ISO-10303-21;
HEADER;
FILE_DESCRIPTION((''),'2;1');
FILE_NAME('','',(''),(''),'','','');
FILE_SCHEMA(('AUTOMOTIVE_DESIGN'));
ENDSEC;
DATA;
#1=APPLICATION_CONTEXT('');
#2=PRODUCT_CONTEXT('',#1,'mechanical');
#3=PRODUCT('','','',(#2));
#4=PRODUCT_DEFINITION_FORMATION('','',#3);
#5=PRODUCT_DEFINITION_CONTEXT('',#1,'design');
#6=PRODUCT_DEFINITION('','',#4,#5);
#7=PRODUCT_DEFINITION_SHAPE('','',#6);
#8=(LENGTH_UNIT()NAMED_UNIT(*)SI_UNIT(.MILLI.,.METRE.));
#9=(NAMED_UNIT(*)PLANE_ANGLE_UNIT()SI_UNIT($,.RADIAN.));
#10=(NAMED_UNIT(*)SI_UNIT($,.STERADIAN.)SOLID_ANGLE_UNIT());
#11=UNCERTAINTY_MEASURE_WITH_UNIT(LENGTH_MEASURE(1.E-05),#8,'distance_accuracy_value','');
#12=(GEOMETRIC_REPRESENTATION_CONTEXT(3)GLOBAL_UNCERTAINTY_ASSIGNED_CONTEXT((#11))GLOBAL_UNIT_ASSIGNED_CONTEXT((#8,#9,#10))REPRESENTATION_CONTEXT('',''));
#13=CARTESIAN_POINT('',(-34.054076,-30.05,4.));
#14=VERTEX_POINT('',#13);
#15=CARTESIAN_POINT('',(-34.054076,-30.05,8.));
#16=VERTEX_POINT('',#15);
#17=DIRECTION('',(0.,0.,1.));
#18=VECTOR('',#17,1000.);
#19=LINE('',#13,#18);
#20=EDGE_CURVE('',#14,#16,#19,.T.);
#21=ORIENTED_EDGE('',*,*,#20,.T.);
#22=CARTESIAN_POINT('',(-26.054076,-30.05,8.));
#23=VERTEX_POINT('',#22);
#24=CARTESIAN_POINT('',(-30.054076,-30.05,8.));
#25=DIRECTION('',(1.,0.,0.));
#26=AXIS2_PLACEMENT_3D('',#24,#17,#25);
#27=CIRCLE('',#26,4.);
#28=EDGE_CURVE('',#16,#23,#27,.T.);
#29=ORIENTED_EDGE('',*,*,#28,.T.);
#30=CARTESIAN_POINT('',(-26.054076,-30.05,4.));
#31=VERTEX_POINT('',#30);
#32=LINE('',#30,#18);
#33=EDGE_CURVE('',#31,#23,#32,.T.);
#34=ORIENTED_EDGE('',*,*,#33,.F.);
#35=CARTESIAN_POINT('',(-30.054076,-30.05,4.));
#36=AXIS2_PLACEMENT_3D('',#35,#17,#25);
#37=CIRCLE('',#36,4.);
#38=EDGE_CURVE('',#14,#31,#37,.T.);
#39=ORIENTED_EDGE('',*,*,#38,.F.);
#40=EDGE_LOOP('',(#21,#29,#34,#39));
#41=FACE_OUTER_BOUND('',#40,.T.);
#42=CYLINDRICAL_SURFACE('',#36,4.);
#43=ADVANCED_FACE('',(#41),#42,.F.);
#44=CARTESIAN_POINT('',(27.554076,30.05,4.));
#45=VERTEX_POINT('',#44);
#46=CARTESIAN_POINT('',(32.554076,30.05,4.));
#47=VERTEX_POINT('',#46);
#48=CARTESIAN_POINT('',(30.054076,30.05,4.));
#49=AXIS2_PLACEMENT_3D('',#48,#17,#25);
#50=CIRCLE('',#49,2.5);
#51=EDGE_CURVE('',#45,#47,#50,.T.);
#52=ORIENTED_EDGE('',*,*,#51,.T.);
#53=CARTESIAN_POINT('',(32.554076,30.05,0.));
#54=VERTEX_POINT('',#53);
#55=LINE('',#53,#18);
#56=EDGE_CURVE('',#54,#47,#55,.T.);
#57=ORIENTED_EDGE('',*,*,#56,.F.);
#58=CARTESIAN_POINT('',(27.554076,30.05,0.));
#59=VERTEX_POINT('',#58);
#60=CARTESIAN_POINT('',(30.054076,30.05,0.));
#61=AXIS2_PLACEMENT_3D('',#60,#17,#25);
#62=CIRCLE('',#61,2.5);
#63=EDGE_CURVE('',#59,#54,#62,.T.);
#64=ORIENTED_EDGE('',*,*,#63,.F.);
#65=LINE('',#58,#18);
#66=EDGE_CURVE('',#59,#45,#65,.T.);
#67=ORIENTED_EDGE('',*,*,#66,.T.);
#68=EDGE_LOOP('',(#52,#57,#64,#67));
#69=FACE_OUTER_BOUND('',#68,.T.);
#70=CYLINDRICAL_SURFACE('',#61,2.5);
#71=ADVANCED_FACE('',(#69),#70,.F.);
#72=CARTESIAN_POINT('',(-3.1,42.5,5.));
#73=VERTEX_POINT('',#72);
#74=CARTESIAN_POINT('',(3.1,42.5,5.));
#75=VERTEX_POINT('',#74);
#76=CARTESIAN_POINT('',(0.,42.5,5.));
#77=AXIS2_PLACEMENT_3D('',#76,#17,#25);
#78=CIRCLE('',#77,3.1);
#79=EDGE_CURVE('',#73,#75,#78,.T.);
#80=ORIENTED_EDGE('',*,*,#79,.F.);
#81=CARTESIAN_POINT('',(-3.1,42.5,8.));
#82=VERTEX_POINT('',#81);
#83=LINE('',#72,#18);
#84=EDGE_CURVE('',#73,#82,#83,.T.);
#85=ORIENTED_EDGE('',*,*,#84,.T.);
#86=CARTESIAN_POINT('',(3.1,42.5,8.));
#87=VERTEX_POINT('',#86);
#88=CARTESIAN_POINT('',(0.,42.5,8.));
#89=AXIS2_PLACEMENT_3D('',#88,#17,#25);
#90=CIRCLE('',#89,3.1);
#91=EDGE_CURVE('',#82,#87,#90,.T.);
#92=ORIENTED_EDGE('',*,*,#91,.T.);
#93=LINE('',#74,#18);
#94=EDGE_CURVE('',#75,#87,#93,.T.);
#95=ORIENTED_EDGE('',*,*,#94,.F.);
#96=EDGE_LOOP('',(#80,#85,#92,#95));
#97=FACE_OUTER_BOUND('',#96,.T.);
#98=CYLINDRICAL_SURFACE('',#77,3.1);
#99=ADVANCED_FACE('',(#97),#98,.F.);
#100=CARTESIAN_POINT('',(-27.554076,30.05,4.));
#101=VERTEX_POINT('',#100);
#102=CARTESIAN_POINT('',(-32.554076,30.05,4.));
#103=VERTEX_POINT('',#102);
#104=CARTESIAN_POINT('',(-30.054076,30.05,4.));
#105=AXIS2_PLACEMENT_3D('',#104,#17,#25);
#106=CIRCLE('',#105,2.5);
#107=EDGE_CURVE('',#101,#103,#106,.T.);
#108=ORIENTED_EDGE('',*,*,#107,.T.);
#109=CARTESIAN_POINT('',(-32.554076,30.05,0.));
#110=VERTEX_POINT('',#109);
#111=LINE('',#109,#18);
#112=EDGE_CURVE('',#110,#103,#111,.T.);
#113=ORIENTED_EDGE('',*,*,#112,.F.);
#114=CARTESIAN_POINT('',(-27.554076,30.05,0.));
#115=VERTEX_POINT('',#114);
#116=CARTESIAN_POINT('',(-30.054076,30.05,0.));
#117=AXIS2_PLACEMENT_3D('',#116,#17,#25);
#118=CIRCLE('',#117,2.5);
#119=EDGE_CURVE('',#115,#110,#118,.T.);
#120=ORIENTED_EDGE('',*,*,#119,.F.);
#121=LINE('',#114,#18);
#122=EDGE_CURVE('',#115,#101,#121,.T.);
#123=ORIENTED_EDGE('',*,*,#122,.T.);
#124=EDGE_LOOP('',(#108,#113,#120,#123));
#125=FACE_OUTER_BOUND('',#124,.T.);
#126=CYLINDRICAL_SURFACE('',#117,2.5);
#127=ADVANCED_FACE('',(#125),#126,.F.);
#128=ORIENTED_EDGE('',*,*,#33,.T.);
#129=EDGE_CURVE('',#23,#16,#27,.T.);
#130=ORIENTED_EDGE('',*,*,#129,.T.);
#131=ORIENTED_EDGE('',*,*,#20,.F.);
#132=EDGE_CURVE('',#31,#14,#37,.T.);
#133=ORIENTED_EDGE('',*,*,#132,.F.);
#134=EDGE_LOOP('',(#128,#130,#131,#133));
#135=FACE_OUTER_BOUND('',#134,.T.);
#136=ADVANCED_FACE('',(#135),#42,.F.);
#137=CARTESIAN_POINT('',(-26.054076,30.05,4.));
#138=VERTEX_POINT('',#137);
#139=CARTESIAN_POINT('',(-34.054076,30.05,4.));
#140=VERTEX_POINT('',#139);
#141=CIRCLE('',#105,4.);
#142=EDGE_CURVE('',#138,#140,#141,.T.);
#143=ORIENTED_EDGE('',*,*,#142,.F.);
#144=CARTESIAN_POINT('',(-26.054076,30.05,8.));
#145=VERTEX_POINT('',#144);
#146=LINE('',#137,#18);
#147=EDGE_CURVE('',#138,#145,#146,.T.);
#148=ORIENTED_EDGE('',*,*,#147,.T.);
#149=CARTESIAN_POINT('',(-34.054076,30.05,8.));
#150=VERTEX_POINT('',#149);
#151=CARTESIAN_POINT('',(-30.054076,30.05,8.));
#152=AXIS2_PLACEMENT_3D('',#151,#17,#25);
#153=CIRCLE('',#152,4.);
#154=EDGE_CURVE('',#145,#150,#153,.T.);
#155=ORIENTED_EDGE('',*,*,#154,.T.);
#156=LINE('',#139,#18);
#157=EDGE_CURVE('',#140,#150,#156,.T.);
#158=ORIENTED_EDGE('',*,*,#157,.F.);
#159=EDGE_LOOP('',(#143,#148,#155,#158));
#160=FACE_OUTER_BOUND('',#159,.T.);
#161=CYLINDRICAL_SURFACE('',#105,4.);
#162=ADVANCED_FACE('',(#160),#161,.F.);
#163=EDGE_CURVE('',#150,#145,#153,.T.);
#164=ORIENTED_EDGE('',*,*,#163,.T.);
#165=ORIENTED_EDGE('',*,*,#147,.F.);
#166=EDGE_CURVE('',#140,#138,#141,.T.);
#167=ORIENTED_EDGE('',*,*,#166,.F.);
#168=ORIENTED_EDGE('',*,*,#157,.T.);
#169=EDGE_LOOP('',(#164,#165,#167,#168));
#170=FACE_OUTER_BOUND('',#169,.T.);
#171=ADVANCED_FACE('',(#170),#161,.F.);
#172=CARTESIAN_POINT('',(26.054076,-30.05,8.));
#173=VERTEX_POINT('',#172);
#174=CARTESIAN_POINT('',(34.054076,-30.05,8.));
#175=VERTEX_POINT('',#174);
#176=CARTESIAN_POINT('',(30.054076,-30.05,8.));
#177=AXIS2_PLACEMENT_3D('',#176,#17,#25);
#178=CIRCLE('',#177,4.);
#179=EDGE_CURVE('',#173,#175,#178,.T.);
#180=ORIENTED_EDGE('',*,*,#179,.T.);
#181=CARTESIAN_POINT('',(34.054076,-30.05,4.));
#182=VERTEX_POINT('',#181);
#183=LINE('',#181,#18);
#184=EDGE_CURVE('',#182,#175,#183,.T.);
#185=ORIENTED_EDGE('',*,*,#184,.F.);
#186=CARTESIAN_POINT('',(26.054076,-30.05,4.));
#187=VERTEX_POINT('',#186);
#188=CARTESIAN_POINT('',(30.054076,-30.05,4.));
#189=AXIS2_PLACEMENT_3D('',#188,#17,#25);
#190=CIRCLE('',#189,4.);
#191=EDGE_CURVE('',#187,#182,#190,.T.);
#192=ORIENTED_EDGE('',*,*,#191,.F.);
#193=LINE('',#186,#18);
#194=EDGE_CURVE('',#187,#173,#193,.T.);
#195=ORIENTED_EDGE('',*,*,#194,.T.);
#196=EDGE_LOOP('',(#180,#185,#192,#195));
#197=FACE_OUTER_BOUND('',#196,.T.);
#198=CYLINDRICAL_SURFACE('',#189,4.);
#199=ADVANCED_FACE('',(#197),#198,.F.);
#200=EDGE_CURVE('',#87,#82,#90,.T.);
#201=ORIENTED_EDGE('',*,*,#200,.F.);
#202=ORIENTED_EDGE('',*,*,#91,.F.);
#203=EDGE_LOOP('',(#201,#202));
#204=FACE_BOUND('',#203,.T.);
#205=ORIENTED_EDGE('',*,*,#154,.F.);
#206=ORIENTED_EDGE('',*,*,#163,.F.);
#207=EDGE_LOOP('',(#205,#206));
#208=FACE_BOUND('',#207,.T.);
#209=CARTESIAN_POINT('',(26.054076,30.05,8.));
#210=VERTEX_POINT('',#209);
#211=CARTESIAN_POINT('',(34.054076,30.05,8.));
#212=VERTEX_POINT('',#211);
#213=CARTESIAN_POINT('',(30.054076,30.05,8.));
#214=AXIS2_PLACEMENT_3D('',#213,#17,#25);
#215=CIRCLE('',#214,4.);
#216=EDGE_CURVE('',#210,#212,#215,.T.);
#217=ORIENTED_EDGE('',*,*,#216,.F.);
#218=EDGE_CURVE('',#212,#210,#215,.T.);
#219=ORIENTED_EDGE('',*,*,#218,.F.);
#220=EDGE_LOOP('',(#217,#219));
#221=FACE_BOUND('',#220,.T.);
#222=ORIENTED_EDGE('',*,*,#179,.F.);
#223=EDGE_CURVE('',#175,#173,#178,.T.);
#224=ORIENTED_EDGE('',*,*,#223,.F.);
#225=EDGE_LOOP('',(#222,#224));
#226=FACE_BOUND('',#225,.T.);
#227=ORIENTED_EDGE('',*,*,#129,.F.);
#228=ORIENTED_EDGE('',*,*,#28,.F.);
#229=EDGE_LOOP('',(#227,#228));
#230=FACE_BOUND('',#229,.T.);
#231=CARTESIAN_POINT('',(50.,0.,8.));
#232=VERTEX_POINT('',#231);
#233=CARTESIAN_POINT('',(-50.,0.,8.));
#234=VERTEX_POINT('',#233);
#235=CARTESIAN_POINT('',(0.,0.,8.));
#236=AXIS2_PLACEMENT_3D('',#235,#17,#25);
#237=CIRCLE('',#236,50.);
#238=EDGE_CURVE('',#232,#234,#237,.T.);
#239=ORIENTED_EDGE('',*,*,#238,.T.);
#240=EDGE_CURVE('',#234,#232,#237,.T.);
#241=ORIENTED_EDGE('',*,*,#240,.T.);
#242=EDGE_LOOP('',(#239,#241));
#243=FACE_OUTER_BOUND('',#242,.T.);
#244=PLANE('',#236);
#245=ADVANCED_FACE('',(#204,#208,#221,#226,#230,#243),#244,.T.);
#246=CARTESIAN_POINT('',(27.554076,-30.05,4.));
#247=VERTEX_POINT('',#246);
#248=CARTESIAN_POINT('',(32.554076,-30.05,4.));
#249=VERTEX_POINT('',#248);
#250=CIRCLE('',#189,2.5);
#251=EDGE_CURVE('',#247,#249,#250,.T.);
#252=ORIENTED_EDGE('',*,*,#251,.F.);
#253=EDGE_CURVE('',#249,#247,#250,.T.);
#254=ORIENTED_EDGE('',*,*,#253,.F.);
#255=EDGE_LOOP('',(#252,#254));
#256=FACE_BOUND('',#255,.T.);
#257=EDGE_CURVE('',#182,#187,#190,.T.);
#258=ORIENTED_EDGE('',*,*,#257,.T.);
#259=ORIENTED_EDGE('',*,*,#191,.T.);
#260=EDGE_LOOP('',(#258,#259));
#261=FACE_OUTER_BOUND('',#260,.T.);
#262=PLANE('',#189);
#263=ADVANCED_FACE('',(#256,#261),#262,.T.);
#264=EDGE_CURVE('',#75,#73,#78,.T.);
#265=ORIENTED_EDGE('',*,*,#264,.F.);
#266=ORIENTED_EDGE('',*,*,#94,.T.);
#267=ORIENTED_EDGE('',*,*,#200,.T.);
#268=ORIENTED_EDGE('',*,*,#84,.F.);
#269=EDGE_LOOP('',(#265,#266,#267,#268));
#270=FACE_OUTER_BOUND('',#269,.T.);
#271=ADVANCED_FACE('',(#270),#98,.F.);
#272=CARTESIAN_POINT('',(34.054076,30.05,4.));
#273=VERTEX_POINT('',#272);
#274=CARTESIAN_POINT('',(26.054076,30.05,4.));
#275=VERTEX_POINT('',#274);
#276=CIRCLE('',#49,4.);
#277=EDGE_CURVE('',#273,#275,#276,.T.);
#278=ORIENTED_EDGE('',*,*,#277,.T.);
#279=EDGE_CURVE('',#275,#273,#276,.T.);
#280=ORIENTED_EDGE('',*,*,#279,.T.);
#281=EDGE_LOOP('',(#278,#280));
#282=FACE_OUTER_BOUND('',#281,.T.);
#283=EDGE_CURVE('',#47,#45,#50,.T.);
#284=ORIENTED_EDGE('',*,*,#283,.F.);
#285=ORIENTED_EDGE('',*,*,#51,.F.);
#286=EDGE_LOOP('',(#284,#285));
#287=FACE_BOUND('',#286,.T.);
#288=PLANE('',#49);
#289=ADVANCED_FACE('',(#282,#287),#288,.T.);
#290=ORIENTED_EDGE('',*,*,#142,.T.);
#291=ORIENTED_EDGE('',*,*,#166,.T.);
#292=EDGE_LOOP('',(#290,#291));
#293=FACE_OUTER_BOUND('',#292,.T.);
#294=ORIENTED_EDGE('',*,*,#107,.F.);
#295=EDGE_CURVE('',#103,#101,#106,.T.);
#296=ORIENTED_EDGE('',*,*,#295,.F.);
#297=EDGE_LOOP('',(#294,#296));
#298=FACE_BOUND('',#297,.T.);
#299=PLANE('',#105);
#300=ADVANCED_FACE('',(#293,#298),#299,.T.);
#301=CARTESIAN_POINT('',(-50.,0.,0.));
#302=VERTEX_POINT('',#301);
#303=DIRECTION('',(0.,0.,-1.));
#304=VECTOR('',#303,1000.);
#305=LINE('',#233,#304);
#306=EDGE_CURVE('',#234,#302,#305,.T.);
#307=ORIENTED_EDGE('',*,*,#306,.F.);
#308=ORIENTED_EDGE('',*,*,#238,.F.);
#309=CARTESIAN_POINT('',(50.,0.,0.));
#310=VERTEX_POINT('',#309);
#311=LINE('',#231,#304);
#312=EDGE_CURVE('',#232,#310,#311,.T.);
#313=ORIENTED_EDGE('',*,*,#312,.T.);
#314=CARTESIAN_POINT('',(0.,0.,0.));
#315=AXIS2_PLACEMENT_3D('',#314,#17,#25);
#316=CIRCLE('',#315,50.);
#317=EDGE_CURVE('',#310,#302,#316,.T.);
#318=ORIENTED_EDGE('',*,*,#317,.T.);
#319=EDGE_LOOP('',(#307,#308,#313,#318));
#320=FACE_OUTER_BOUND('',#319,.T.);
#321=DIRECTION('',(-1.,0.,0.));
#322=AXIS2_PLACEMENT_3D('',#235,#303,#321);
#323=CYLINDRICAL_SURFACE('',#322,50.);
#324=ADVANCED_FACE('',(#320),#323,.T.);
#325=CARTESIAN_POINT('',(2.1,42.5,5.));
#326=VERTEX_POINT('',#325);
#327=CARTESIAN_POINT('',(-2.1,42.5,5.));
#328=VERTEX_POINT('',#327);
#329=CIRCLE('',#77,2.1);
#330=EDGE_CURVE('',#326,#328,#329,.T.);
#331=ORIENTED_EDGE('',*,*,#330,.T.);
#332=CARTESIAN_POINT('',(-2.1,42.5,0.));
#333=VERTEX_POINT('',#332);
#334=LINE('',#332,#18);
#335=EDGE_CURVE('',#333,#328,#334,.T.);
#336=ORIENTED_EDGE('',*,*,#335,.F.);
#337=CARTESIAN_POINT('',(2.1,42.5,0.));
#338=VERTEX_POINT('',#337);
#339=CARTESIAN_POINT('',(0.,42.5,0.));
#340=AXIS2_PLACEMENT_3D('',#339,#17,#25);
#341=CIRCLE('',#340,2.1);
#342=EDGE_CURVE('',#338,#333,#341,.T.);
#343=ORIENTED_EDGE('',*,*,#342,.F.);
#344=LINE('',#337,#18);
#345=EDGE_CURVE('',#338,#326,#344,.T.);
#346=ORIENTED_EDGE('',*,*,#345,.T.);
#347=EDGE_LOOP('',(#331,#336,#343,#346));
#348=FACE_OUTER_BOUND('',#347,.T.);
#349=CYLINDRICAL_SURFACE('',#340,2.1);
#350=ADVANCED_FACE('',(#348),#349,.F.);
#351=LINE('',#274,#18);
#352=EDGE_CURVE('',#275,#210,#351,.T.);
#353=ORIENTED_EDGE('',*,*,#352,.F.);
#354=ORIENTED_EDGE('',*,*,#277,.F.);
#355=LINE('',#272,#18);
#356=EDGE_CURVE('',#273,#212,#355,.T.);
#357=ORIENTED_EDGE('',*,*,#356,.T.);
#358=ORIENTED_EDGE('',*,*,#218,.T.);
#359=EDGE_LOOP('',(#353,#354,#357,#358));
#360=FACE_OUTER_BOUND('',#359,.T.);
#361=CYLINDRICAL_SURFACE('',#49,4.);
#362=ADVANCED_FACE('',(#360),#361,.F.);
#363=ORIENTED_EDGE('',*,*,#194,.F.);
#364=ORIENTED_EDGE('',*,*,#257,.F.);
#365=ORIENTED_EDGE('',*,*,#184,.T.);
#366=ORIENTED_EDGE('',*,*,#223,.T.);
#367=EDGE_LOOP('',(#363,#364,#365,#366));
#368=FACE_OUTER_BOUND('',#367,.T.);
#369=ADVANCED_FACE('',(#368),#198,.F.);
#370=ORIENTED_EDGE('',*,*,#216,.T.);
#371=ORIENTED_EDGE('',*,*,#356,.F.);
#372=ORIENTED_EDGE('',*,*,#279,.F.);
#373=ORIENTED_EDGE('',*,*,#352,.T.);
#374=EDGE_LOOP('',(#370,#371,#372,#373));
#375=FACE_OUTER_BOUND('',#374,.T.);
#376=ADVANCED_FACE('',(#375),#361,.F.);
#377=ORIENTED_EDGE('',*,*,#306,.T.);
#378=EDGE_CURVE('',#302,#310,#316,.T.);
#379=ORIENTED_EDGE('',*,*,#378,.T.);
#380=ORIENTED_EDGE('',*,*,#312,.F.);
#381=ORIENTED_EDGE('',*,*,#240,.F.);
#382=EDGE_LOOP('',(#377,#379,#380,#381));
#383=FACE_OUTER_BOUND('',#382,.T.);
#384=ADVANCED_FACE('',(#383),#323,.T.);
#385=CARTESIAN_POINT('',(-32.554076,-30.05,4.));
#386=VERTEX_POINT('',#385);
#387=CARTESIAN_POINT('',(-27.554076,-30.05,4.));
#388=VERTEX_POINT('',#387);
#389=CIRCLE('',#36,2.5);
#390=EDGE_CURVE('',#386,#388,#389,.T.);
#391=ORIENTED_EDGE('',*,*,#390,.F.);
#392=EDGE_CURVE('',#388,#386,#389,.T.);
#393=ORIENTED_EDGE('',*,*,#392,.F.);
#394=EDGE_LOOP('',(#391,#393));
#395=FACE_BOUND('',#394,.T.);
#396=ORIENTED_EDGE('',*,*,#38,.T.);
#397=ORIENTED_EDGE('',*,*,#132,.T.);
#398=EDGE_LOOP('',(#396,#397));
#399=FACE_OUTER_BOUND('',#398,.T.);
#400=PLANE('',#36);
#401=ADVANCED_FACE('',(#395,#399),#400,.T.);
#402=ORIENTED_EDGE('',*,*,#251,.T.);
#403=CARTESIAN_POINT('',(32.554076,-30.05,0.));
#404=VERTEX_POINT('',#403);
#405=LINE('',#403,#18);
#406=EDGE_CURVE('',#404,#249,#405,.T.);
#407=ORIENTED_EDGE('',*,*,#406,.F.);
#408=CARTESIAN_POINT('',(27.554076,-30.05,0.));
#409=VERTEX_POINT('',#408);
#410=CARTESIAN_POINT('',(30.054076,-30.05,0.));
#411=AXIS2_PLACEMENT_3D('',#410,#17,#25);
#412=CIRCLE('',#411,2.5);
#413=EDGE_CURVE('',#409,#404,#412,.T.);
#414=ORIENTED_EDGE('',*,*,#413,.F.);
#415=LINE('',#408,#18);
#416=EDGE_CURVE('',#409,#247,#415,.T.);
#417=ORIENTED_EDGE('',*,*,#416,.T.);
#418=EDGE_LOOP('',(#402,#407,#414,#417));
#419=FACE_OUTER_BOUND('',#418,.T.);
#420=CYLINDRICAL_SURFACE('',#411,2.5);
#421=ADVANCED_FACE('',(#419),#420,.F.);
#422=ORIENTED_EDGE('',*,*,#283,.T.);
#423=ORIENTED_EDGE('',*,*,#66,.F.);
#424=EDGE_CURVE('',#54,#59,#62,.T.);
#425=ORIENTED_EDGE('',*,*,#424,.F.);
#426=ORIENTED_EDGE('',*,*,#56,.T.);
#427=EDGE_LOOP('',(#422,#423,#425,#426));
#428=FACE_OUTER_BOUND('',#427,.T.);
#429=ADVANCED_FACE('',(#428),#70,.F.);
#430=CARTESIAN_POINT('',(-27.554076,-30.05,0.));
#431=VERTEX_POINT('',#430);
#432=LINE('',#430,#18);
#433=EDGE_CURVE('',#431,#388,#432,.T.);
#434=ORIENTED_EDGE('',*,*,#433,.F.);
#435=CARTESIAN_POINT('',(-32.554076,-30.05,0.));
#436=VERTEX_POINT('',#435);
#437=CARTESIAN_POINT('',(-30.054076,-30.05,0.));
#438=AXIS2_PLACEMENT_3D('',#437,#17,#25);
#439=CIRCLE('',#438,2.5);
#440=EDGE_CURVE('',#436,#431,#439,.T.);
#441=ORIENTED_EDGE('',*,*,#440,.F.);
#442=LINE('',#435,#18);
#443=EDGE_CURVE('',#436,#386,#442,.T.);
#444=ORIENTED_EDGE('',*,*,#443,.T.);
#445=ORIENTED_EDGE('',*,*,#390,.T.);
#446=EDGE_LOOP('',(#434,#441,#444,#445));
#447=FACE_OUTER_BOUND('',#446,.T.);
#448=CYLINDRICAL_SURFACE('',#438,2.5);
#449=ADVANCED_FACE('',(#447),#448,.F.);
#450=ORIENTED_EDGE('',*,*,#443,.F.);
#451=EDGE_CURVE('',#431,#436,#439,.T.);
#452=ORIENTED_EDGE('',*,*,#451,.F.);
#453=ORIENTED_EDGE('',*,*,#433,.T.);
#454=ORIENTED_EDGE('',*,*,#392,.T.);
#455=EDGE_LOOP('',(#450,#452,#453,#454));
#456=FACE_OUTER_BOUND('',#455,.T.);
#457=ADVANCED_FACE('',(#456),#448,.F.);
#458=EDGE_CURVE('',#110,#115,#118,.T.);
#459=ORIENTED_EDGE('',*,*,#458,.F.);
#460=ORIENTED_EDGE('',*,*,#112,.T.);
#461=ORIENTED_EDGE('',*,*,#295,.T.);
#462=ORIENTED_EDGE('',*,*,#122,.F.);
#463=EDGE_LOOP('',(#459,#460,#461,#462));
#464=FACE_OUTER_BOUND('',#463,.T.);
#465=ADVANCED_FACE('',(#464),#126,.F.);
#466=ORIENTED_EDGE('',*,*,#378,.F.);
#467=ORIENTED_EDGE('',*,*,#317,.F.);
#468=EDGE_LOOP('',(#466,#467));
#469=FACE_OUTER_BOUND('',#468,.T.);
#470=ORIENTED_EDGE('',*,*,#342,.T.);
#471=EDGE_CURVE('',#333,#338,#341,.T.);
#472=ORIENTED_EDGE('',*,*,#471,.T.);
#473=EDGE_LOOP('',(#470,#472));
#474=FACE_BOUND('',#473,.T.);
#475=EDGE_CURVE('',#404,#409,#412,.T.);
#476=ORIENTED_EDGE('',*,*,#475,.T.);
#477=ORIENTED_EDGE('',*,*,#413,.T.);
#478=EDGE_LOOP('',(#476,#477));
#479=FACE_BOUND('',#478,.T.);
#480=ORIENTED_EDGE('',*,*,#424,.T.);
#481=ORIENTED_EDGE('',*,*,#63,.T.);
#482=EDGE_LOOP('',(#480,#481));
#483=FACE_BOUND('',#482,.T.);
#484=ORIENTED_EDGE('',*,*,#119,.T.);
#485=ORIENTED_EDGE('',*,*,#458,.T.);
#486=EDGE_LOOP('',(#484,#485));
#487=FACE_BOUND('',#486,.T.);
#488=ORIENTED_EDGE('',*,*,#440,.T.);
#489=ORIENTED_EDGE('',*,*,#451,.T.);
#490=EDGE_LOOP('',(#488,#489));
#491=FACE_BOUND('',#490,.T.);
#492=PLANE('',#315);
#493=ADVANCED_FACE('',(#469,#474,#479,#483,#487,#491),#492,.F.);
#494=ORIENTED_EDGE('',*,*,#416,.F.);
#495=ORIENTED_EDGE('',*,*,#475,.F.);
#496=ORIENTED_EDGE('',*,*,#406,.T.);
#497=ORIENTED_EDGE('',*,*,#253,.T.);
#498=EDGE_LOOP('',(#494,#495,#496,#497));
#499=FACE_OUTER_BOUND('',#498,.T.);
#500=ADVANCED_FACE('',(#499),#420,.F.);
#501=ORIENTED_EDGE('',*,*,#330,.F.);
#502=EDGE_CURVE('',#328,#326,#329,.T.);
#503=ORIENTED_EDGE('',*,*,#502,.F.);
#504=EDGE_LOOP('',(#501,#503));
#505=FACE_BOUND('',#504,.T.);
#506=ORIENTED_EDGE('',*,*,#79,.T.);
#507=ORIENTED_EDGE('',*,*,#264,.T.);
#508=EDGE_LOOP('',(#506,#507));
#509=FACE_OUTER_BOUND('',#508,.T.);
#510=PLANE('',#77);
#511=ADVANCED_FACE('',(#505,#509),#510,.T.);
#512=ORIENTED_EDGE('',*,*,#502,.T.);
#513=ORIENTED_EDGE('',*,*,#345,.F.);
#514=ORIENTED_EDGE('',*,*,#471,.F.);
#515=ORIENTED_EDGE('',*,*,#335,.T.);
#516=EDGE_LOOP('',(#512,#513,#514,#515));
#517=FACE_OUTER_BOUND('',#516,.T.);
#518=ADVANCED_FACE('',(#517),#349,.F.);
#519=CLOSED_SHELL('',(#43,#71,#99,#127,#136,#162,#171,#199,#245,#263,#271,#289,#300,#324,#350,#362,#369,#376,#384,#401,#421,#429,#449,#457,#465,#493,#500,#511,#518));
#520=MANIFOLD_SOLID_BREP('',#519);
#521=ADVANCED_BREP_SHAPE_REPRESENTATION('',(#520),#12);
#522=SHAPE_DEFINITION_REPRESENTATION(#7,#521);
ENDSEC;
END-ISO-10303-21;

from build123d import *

# Parameters (mm, degrees)
SKETCH1_R           = 50
BOSS_EXTRUDE1_DEPTH = 8
SKETCH2_R           = 4
CUT_EXTRUDE1_DEPTH  = 4
SKETCH3_R           = 3.1
CUT_EXTRUDE2_DEPTH  = 3
SKETCH4_R           = 2.5
SKETCH4_R_2         = 2.1
CUT_EXTRUDE3_DEPTH  = 71.823724839
SKETCH5_R           = 2.1
CUT_EXTRUDE4_DEPTH  = 5


with BuildPart() as part:
    # Sketch1 → Boss-Extrude1 (new body)
    with BuildSketch(Plane.XY):
        Circle(SKETCH1_R)
    extrude(amount=BOSS_EXTRUDE1_DEPTH)

    # Sketch2 → Cut-Extrude1 (cut)
    with BuildSketch(Plane.XY.offset(8)):
        with Locations((-30.054076263, 30.05)):
            Circle(SKETCH2_R)
        with Locations((30.054076263, 30.05)):
            Circle(SKETCH2_R)
        with Locations((-30.054076263, -30.05)):
            Circle(SKETCH2_R)
        with Locations((30.054076263, -30.05)):
            Circle(SKETCH2_R)
    extrude(amount=-CUT_EXTRUDE1_DEPTH, mode=Mode.SUBTRACT)

    # Sketch3 → Cut-Extrude2 (cut)
    with BuildSketch(Plane.XY.offset(8)):
        with Locations((0, 42.5)):
            Circle(SKETCH3_R)
    extrude(amount=-CUT_EXTRUDE2_DEPTH, mode=Mode.SUBTRACT)

    # Sketch4 → Cut-Extrude3 (cut, through all)
    with BuildSketch(Plane.XY.offset(4)):
        with Locations((-30.054076263, 30.05)):
            Circle(SKETCH4_R)
        with Locations((30.054076263, 30.05)):
            Circle(SKETCH4_R)
        with Locations((-30.054076263, -30.05)):
            Circle(SKETCH4_R)
        with Locations((30.054076263, -30.05)):
            Circle(SKETCH4_R)
        with Locations((0, 42.5)):
            Circle(SKETCH4_R_2)
    extrude(amount=-CUT_EXTRUDE3_DEPTH, mode=Mode.SUBTRACT)

    # Sketch5 → Cut-Extrude4 (cut)
    with BuildSketch(Plane.XY.offset(5)):
        with Locations((0, 42.5)):
            Circle(SKETCH5_R)
    extrude(amount=-CUT_EXTRUDE4_DEPTH, mode=Mode.SUBTRACT)


solid = part.part
